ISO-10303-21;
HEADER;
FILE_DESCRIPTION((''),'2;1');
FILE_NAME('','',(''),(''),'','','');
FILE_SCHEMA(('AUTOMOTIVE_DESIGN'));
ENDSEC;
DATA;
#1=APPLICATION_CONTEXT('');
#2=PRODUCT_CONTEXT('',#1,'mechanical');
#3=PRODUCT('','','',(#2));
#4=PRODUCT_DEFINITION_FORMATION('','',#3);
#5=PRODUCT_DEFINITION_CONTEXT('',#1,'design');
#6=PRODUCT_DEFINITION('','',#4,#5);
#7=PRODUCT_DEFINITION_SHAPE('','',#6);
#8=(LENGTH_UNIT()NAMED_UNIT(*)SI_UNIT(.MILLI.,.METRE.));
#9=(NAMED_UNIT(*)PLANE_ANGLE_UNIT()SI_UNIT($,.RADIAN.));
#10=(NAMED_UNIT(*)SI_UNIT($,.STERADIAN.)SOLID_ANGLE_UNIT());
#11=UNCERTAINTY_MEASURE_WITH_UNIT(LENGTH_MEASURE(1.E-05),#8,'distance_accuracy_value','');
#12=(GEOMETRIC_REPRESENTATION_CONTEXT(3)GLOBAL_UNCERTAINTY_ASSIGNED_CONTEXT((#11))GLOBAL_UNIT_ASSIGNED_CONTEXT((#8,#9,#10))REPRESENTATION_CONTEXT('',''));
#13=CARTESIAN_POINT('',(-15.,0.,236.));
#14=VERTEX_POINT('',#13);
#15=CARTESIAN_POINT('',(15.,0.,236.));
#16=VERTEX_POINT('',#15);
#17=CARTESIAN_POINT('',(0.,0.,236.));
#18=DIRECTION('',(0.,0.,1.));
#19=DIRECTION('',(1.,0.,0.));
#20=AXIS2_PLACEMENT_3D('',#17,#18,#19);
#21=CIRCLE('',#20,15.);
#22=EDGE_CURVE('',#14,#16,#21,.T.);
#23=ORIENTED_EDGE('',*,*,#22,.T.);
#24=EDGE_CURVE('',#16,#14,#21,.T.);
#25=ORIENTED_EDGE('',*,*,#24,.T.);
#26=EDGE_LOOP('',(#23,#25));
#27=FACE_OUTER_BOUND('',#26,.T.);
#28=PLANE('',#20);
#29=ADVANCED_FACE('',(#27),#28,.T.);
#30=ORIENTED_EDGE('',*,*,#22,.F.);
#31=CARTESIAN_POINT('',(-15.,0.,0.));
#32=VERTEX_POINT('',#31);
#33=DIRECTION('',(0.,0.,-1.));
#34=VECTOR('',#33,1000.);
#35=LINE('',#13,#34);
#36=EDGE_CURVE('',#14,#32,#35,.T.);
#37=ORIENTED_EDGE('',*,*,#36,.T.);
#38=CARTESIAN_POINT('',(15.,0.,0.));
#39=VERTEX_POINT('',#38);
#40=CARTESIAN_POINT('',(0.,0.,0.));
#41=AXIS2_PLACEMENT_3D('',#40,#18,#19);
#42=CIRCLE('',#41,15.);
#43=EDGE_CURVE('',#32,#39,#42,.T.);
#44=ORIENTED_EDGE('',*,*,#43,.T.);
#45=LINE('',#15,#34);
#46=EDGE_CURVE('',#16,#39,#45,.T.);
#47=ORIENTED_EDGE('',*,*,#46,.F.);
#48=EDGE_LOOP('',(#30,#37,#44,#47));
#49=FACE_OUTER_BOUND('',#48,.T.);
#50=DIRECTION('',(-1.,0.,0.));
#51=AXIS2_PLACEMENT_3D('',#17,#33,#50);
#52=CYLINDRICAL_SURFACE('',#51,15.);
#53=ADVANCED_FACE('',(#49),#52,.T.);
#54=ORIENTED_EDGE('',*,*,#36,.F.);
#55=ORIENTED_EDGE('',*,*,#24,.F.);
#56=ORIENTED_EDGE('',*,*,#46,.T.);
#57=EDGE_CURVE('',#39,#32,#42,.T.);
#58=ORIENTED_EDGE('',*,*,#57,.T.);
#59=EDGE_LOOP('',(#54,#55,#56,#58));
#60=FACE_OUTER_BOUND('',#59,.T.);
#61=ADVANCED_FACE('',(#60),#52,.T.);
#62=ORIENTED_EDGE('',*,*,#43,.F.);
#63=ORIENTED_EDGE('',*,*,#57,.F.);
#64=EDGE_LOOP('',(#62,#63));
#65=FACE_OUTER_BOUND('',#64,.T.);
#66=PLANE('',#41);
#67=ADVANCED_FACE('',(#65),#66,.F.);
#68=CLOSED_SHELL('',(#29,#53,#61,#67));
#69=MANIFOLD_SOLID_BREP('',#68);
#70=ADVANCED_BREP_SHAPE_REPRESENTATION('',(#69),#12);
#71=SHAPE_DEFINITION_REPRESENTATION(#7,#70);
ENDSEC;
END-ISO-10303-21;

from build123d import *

# Parameters (mm, degrees)
SKETCH_1_R      = 15
EXTRUDE_1_DEPTH = 236


with BuildPart() as part:
    # 草图1 → 凸台-拉伸1 (new body)
    with BuildSketch(Plane.XY):
        with Locations(Location((0, 0, 0), (0, 0, 180))):
            Circle(SKETCH_1_R)
    extrude(amount=EXTRUDE_1_DEPTH)


solid = part.part
